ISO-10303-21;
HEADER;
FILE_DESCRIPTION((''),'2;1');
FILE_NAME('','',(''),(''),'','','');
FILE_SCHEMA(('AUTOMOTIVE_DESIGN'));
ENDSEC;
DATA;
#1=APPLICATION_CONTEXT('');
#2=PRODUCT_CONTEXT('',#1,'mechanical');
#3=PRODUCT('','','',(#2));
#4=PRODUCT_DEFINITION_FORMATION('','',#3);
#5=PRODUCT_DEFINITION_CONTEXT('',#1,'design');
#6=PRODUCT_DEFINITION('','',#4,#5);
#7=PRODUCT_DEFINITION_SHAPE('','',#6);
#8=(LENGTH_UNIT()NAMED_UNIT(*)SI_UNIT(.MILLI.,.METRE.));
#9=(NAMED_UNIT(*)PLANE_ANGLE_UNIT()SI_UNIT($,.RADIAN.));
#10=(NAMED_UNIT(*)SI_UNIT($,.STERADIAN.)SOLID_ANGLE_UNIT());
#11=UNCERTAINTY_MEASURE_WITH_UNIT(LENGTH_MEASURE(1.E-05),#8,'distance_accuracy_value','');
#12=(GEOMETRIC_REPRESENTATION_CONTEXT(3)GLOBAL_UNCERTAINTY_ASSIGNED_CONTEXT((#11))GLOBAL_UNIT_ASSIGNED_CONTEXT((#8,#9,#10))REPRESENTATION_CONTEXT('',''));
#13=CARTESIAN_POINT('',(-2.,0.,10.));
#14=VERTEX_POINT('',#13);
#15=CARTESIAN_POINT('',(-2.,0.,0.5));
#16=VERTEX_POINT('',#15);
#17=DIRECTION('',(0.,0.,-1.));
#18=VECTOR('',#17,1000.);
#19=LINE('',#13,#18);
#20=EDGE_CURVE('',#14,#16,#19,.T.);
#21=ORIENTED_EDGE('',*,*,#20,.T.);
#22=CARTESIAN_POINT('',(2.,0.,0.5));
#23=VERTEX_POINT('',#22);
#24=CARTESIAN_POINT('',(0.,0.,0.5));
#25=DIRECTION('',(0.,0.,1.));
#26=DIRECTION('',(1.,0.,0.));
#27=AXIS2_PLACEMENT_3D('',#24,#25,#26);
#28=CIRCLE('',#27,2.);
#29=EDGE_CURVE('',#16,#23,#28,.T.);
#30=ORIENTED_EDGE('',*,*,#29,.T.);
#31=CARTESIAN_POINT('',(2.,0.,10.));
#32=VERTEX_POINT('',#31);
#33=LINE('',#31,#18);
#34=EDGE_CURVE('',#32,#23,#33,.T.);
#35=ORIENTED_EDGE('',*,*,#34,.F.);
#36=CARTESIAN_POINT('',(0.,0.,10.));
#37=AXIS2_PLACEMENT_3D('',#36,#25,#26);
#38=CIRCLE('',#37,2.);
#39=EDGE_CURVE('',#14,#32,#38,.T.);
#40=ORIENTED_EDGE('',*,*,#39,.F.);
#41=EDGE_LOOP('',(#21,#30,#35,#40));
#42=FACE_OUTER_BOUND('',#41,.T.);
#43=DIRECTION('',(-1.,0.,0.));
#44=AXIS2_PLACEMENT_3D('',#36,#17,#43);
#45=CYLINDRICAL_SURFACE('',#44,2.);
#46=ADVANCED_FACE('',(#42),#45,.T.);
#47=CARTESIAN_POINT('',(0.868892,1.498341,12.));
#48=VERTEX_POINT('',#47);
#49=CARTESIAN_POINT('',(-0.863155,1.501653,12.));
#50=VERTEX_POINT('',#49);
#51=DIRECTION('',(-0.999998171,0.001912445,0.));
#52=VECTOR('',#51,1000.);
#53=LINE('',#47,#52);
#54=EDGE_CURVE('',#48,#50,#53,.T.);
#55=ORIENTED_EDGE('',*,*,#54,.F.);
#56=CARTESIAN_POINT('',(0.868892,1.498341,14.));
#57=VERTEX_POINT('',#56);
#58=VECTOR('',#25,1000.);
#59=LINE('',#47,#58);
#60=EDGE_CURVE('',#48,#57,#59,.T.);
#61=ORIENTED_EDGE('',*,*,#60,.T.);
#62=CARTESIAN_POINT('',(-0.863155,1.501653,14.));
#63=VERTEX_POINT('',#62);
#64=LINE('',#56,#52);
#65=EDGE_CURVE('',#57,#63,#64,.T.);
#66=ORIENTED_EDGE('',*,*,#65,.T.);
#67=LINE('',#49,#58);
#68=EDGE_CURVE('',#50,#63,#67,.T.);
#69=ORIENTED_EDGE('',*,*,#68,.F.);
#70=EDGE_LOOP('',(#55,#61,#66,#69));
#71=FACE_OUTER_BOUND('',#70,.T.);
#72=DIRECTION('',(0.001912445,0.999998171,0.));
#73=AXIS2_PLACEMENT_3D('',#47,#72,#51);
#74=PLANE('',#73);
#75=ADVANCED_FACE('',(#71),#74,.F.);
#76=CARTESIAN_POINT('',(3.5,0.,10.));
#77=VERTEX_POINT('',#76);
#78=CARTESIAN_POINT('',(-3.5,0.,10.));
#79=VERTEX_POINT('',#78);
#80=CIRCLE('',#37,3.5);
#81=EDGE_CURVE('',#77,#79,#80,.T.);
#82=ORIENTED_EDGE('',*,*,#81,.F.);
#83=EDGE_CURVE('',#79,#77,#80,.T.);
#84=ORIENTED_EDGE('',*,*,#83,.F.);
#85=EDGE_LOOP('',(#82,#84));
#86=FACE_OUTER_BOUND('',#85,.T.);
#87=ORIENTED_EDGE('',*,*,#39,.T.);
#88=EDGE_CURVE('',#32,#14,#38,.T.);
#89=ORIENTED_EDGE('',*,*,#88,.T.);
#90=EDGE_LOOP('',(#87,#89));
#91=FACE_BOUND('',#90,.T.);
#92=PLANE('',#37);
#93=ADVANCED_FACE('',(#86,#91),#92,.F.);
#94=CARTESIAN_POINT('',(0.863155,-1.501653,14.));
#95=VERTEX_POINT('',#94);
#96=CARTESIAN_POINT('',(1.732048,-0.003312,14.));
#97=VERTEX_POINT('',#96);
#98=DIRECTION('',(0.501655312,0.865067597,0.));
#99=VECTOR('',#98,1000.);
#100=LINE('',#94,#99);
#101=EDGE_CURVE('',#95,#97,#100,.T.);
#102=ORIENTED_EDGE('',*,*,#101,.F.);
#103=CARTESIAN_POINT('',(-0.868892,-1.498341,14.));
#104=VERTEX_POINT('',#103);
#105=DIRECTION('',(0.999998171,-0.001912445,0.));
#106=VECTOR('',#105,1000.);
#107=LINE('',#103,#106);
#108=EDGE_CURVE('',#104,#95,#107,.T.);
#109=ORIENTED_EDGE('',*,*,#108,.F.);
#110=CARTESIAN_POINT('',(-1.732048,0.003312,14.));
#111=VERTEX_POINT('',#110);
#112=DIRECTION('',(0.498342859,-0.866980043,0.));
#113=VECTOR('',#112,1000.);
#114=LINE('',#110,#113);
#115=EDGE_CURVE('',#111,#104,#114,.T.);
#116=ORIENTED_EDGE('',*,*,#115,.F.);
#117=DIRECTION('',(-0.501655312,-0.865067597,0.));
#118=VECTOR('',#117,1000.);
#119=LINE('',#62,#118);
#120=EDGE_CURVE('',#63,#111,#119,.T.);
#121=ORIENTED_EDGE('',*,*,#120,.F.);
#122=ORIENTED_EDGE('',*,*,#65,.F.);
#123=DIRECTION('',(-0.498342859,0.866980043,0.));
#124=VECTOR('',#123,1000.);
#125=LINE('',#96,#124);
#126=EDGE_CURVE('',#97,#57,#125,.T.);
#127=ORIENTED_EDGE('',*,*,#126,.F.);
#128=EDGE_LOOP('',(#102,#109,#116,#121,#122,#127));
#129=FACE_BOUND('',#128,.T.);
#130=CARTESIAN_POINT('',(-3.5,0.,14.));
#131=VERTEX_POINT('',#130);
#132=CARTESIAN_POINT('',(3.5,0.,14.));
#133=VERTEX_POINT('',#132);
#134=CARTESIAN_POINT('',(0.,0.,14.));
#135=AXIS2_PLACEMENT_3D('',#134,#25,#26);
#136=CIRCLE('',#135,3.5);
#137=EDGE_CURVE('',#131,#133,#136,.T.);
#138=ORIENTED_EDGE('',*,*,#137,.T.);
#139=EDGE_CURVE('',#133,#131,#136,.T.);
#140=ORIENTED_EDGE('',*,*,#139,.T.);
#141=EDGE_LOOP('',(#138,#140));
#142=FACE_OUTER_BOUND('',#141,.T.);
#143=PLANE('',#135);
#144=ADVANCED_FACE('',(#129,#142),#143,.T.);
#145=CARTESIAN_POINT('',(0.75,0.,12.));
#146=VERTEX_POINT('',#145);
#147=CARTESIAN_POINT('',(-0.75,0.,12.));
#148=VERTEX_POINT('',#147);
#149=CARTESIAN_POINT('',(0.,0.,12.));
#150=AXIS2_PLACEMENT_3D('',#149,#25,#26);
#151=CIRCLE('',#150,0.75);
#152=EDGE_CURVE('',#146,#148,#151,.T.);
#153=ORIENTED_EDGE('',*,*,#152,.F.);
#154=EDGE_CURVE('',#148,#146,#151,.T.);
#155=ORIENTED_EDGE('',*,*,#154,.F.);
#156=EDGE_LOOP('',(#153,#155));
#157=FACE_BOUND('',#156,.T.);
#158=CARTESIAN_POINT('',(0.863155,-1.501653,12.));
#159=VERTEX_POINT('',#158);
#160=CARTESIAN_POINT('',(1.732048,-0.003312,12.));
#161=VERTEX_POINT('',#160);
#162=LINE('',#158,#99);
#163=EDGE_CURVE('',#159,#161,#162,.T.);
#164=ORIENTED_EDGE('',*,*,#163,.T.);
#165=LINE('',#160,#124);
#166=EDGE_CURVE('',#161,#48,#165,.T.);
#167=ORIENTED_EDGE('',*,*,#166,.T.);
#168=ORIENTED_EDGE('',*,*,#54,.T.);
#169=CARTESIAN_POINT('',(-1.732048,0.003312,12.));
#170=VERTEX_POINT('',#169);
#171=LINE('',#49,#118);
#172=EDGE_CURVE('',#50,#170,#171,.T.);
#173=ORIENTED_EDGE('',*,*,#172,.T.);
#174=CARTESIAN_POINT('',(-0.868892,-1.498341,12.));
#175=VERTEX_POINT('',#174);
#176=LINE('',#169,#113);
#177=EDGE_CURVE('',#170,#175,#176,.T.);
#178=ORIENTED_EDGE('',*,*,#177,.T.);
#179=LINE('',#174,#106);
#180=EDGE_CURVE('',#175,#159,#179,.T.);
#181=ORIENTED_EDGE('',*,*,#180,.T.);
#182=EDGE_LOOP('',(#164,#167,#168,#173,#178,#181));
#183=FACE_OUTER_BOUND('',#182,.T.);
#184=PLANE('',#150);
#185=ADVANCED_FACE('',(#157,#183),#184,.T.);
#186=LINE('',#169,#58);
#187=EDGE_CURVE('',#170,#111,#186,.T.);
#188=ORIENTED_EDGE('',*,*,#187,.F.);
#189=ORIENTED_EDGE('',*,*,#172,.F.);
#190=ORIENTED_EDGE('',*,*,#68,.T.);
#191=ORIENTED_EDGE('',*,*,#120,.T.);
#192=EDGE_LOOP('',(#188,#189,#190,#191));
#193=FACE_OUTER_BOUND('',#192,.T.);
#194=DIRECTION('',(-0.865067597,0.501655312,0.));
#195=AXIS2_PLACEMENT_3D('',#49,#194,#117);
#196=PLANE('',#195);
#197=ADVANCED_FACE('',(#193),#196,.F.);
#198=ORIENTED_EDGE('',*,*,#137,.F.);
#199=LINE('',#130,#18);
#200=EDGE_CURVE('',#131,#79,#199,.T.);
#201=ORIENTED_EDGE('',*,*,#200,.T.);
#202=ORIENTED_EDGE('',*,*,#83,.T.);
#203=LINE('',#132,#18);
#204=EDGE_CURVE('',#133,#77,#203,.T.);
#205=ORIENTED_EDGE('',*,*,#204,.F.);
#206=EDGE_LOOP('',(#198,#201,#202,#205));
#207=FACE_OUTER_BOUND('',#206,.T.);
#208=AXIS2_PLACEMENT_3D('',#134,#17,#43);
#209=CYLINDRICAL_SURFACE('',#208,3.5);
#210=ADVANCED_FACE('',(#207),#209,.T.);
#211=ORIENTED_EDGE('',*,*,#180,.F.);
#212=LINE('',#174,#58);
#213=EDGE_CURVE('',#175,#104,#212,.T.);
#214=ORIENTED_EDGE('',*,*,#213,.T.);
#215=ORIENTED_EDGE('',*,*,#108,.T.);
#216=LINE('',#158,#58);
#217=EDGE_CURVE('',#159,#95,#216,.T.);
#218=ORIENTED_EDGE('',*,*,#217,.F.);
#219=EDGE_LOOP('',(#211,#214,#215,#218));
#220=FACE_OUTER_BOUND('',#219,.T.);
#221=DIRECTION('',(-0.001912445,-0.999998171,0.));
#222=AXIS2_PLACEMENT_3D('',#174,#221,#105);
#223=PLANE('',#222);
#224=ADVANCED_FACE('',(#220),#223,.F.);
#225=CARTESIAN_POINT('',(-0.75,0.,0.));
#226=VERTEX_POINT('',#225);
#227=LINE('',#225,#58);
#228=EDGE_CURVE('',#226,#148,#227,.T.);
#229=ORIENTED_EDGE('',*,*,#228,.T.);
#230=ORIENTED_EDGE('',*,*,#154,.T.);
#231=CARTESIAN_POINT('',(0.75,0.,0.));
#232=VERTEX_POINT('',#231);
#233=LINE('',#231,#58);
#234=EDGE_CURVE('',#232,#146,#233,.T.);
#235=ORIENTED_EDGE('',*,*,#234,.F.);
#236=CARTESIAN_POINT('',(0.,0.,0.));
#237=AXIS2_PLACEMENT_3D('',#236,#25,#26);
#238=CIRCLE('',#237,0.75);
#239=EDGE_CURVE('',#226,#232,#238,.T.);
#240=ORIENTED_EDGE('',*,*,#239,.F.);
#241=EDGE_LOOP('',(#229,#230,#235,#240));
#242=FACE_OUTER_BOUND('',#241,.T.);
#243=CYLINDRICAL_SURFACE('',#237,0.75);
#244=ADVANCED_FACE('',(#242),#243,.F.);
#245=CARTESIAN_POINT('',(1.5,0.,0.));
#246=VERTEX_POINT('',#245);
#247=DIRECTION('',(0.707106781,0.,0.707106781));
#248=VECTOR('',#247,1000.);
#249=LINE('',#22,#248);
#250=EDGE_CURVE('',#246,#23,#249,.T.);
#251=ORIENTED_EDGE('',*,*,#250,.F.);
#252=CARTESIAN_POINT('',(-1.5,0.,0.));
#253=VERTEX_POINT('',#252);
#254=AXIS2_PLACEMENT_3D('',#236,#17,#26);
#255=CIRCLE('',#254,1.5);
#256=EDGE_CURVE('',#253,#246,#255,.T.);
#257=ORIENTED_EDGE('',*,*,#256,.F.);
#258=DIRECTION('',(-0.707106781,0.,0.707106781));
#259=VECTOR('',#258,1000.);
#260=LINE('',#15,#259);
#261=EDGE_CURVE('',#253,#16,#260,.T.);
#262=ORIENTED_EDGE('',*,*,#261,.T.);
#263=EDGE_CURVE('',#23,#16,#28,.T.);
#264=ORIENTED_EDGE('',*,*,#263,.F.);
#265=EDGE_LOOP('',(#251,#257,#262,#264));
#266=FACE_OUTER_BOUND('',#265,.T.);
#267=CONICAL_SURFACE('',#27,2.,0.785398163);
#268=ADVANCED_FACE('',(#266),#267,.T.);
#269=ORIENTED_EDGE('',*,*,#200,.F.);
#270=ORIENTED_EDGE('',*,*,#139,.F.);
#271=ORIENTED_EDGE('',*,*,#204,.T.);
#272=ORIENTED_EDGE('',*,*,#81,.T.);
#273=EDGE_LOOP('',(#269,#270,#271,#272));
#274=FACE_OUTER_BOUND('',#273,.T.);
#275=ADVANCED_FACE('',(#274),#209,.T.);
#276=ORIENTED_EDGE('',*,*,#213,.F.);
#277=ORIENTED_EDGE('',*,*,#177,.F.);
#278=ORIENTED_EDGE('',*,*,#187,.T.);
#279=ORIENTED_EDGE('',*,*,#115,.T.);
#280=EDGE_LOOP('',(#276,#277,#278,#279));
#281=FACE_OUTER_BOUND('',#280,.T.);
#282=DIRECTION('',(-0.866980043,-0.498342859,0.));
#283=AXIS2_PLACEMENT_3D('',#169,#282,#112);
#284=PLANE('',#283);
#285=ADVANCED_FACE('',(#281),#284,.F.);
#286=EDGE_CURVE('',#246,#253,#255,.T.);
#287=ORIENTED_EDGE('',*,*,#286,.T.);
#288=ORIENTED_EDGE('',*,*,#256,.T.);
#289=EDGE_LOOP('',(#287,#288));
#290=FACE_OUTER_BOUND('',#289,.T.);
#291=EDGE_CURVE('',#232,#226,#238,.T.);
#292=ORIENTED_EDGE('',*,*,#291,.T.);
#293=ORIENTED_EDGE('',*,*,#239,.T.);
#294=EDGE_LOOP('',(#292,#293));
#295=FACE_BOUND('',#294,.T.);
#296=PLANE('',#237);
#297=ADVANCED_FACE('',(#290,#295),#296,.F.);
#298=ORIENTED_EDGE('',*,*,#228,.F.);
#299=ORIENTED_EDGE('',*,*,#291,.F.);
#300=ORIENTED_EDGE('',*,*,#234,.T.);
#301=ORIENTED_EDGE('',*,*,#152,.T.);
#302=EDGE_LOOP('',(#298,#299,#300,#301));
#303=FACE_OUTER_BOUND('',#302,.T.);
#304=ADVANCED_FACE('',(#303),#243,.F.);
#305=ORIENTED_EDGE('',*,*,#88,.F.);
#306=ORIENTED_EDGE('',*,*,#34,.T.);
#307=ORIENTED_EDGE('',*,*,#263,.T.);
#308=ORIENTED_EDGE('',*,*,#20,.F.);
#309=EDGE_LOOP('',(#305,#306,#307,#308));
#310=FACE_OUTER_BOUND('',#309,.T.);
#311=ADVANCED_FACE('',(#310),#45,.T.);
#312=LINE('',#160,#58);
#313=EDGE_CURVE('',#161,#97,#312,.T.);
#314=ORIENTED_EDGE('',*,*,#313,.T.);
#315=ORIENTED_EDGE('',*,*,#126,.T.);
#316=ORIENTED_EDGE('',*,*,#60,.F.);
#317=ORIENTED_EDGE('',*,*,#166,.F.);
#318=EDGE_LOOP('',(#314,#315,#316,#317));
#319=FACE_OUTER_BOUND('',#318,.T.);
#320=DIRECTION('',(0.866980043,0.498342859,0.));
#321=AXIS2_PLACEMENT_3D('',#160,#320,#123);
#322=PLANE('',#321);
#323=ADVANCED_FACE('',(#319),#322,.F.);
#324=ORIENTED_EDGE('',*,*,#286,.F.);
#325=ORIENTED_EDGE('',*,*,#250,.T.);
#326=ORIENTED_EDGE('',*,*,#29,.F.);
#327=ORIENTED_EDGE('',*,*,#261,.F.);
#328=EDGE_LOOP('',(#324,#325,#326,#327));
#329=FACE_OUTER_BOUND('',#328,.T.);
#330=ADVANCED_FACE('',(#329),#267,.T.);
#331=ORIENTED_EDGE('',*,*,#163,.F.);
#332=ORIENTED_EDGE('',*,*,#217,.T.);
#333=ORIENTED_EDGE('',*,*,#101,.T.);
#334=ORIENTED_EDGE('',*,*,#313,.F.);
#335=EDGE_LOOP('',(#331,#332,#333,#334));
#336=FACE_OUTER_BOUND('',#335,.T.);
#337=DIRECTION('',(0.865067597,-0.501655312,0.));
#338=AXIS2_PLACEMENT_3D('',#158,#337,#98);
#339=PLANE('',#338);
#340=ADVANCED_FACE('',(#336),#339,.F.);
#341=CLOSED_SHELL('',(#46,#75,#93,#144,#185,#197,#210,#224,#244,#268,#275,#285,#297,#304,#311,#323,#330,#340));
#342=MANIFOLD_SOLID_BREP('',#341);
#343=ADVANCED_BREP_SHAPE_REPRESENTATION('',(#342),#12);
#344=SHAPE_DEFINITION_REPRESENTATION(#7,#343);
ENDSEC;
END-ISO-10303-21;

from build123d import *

# Parameters (mm, degrees)
SKETCH_1_R          = 2
EXTRUDE_1_DEPTH     = 10
SKETCH_2_R          = 3.5
EXTRUDE_2_DEPTH     = 4
CUT_EXTRUDE_1_DEPTH = 2
CHAMFER_1_SIZE      = 0.5
SKETCH_4_R          = 0.75
CUT_EXTRUDE_2_DEPTH = 13.980754986


with BuildPart() as part:
    # 草图1 → 凸台-拉伸1 (new body)
    with BuildSketch(Plane.XY):
        Circle(SKETCH_1_R)
    extrude(amount=EXTRUDE_1_DEPTH)

    # 草图2 → 凸台-拉伸2 (add)
    with BuildSketch(Plane.XY.offset(10)):
        Circle(SKETCH_2_R)
    extrude(amount=EXTRUDE_2_DEPTH)

    # 草图3 → 切除-拉伸1 (cut)
    with BuildSketch(Plane.XY.offset(14)):
        Polygon((-0.863155152, 1.501653483), (-1.73204764, 0.003312453), (-0.868892488, -1.498341031), (0.863155152, -1.501653483), (1.73204764, -0.003312453), (0.868892488, 1.498341031), align=None)
    extrude(amount=-CUT_EXTRUDE_1_DEPTH, mode=Mode.SUBTRACT)

    # 倒角1
    chamfer_1_edges = [part.edges().sort_by_distance(p)[0] for p in [
        (-2, 0, 0),
    ]]
    chamfer(chamfer_1_edges, length=CHAMFER_1_SIZE)

    # 草图4 → 切除-拉伸2 (cut, through all)
    with BuildSketch(Plane.XY.offset(12)):
        Circle(SKETCH_4_R)
    extrude(amount=-CUT_EXTRUDE_2_DEPTH, mode=Mode.SUBTRACT)


solid = part.part
